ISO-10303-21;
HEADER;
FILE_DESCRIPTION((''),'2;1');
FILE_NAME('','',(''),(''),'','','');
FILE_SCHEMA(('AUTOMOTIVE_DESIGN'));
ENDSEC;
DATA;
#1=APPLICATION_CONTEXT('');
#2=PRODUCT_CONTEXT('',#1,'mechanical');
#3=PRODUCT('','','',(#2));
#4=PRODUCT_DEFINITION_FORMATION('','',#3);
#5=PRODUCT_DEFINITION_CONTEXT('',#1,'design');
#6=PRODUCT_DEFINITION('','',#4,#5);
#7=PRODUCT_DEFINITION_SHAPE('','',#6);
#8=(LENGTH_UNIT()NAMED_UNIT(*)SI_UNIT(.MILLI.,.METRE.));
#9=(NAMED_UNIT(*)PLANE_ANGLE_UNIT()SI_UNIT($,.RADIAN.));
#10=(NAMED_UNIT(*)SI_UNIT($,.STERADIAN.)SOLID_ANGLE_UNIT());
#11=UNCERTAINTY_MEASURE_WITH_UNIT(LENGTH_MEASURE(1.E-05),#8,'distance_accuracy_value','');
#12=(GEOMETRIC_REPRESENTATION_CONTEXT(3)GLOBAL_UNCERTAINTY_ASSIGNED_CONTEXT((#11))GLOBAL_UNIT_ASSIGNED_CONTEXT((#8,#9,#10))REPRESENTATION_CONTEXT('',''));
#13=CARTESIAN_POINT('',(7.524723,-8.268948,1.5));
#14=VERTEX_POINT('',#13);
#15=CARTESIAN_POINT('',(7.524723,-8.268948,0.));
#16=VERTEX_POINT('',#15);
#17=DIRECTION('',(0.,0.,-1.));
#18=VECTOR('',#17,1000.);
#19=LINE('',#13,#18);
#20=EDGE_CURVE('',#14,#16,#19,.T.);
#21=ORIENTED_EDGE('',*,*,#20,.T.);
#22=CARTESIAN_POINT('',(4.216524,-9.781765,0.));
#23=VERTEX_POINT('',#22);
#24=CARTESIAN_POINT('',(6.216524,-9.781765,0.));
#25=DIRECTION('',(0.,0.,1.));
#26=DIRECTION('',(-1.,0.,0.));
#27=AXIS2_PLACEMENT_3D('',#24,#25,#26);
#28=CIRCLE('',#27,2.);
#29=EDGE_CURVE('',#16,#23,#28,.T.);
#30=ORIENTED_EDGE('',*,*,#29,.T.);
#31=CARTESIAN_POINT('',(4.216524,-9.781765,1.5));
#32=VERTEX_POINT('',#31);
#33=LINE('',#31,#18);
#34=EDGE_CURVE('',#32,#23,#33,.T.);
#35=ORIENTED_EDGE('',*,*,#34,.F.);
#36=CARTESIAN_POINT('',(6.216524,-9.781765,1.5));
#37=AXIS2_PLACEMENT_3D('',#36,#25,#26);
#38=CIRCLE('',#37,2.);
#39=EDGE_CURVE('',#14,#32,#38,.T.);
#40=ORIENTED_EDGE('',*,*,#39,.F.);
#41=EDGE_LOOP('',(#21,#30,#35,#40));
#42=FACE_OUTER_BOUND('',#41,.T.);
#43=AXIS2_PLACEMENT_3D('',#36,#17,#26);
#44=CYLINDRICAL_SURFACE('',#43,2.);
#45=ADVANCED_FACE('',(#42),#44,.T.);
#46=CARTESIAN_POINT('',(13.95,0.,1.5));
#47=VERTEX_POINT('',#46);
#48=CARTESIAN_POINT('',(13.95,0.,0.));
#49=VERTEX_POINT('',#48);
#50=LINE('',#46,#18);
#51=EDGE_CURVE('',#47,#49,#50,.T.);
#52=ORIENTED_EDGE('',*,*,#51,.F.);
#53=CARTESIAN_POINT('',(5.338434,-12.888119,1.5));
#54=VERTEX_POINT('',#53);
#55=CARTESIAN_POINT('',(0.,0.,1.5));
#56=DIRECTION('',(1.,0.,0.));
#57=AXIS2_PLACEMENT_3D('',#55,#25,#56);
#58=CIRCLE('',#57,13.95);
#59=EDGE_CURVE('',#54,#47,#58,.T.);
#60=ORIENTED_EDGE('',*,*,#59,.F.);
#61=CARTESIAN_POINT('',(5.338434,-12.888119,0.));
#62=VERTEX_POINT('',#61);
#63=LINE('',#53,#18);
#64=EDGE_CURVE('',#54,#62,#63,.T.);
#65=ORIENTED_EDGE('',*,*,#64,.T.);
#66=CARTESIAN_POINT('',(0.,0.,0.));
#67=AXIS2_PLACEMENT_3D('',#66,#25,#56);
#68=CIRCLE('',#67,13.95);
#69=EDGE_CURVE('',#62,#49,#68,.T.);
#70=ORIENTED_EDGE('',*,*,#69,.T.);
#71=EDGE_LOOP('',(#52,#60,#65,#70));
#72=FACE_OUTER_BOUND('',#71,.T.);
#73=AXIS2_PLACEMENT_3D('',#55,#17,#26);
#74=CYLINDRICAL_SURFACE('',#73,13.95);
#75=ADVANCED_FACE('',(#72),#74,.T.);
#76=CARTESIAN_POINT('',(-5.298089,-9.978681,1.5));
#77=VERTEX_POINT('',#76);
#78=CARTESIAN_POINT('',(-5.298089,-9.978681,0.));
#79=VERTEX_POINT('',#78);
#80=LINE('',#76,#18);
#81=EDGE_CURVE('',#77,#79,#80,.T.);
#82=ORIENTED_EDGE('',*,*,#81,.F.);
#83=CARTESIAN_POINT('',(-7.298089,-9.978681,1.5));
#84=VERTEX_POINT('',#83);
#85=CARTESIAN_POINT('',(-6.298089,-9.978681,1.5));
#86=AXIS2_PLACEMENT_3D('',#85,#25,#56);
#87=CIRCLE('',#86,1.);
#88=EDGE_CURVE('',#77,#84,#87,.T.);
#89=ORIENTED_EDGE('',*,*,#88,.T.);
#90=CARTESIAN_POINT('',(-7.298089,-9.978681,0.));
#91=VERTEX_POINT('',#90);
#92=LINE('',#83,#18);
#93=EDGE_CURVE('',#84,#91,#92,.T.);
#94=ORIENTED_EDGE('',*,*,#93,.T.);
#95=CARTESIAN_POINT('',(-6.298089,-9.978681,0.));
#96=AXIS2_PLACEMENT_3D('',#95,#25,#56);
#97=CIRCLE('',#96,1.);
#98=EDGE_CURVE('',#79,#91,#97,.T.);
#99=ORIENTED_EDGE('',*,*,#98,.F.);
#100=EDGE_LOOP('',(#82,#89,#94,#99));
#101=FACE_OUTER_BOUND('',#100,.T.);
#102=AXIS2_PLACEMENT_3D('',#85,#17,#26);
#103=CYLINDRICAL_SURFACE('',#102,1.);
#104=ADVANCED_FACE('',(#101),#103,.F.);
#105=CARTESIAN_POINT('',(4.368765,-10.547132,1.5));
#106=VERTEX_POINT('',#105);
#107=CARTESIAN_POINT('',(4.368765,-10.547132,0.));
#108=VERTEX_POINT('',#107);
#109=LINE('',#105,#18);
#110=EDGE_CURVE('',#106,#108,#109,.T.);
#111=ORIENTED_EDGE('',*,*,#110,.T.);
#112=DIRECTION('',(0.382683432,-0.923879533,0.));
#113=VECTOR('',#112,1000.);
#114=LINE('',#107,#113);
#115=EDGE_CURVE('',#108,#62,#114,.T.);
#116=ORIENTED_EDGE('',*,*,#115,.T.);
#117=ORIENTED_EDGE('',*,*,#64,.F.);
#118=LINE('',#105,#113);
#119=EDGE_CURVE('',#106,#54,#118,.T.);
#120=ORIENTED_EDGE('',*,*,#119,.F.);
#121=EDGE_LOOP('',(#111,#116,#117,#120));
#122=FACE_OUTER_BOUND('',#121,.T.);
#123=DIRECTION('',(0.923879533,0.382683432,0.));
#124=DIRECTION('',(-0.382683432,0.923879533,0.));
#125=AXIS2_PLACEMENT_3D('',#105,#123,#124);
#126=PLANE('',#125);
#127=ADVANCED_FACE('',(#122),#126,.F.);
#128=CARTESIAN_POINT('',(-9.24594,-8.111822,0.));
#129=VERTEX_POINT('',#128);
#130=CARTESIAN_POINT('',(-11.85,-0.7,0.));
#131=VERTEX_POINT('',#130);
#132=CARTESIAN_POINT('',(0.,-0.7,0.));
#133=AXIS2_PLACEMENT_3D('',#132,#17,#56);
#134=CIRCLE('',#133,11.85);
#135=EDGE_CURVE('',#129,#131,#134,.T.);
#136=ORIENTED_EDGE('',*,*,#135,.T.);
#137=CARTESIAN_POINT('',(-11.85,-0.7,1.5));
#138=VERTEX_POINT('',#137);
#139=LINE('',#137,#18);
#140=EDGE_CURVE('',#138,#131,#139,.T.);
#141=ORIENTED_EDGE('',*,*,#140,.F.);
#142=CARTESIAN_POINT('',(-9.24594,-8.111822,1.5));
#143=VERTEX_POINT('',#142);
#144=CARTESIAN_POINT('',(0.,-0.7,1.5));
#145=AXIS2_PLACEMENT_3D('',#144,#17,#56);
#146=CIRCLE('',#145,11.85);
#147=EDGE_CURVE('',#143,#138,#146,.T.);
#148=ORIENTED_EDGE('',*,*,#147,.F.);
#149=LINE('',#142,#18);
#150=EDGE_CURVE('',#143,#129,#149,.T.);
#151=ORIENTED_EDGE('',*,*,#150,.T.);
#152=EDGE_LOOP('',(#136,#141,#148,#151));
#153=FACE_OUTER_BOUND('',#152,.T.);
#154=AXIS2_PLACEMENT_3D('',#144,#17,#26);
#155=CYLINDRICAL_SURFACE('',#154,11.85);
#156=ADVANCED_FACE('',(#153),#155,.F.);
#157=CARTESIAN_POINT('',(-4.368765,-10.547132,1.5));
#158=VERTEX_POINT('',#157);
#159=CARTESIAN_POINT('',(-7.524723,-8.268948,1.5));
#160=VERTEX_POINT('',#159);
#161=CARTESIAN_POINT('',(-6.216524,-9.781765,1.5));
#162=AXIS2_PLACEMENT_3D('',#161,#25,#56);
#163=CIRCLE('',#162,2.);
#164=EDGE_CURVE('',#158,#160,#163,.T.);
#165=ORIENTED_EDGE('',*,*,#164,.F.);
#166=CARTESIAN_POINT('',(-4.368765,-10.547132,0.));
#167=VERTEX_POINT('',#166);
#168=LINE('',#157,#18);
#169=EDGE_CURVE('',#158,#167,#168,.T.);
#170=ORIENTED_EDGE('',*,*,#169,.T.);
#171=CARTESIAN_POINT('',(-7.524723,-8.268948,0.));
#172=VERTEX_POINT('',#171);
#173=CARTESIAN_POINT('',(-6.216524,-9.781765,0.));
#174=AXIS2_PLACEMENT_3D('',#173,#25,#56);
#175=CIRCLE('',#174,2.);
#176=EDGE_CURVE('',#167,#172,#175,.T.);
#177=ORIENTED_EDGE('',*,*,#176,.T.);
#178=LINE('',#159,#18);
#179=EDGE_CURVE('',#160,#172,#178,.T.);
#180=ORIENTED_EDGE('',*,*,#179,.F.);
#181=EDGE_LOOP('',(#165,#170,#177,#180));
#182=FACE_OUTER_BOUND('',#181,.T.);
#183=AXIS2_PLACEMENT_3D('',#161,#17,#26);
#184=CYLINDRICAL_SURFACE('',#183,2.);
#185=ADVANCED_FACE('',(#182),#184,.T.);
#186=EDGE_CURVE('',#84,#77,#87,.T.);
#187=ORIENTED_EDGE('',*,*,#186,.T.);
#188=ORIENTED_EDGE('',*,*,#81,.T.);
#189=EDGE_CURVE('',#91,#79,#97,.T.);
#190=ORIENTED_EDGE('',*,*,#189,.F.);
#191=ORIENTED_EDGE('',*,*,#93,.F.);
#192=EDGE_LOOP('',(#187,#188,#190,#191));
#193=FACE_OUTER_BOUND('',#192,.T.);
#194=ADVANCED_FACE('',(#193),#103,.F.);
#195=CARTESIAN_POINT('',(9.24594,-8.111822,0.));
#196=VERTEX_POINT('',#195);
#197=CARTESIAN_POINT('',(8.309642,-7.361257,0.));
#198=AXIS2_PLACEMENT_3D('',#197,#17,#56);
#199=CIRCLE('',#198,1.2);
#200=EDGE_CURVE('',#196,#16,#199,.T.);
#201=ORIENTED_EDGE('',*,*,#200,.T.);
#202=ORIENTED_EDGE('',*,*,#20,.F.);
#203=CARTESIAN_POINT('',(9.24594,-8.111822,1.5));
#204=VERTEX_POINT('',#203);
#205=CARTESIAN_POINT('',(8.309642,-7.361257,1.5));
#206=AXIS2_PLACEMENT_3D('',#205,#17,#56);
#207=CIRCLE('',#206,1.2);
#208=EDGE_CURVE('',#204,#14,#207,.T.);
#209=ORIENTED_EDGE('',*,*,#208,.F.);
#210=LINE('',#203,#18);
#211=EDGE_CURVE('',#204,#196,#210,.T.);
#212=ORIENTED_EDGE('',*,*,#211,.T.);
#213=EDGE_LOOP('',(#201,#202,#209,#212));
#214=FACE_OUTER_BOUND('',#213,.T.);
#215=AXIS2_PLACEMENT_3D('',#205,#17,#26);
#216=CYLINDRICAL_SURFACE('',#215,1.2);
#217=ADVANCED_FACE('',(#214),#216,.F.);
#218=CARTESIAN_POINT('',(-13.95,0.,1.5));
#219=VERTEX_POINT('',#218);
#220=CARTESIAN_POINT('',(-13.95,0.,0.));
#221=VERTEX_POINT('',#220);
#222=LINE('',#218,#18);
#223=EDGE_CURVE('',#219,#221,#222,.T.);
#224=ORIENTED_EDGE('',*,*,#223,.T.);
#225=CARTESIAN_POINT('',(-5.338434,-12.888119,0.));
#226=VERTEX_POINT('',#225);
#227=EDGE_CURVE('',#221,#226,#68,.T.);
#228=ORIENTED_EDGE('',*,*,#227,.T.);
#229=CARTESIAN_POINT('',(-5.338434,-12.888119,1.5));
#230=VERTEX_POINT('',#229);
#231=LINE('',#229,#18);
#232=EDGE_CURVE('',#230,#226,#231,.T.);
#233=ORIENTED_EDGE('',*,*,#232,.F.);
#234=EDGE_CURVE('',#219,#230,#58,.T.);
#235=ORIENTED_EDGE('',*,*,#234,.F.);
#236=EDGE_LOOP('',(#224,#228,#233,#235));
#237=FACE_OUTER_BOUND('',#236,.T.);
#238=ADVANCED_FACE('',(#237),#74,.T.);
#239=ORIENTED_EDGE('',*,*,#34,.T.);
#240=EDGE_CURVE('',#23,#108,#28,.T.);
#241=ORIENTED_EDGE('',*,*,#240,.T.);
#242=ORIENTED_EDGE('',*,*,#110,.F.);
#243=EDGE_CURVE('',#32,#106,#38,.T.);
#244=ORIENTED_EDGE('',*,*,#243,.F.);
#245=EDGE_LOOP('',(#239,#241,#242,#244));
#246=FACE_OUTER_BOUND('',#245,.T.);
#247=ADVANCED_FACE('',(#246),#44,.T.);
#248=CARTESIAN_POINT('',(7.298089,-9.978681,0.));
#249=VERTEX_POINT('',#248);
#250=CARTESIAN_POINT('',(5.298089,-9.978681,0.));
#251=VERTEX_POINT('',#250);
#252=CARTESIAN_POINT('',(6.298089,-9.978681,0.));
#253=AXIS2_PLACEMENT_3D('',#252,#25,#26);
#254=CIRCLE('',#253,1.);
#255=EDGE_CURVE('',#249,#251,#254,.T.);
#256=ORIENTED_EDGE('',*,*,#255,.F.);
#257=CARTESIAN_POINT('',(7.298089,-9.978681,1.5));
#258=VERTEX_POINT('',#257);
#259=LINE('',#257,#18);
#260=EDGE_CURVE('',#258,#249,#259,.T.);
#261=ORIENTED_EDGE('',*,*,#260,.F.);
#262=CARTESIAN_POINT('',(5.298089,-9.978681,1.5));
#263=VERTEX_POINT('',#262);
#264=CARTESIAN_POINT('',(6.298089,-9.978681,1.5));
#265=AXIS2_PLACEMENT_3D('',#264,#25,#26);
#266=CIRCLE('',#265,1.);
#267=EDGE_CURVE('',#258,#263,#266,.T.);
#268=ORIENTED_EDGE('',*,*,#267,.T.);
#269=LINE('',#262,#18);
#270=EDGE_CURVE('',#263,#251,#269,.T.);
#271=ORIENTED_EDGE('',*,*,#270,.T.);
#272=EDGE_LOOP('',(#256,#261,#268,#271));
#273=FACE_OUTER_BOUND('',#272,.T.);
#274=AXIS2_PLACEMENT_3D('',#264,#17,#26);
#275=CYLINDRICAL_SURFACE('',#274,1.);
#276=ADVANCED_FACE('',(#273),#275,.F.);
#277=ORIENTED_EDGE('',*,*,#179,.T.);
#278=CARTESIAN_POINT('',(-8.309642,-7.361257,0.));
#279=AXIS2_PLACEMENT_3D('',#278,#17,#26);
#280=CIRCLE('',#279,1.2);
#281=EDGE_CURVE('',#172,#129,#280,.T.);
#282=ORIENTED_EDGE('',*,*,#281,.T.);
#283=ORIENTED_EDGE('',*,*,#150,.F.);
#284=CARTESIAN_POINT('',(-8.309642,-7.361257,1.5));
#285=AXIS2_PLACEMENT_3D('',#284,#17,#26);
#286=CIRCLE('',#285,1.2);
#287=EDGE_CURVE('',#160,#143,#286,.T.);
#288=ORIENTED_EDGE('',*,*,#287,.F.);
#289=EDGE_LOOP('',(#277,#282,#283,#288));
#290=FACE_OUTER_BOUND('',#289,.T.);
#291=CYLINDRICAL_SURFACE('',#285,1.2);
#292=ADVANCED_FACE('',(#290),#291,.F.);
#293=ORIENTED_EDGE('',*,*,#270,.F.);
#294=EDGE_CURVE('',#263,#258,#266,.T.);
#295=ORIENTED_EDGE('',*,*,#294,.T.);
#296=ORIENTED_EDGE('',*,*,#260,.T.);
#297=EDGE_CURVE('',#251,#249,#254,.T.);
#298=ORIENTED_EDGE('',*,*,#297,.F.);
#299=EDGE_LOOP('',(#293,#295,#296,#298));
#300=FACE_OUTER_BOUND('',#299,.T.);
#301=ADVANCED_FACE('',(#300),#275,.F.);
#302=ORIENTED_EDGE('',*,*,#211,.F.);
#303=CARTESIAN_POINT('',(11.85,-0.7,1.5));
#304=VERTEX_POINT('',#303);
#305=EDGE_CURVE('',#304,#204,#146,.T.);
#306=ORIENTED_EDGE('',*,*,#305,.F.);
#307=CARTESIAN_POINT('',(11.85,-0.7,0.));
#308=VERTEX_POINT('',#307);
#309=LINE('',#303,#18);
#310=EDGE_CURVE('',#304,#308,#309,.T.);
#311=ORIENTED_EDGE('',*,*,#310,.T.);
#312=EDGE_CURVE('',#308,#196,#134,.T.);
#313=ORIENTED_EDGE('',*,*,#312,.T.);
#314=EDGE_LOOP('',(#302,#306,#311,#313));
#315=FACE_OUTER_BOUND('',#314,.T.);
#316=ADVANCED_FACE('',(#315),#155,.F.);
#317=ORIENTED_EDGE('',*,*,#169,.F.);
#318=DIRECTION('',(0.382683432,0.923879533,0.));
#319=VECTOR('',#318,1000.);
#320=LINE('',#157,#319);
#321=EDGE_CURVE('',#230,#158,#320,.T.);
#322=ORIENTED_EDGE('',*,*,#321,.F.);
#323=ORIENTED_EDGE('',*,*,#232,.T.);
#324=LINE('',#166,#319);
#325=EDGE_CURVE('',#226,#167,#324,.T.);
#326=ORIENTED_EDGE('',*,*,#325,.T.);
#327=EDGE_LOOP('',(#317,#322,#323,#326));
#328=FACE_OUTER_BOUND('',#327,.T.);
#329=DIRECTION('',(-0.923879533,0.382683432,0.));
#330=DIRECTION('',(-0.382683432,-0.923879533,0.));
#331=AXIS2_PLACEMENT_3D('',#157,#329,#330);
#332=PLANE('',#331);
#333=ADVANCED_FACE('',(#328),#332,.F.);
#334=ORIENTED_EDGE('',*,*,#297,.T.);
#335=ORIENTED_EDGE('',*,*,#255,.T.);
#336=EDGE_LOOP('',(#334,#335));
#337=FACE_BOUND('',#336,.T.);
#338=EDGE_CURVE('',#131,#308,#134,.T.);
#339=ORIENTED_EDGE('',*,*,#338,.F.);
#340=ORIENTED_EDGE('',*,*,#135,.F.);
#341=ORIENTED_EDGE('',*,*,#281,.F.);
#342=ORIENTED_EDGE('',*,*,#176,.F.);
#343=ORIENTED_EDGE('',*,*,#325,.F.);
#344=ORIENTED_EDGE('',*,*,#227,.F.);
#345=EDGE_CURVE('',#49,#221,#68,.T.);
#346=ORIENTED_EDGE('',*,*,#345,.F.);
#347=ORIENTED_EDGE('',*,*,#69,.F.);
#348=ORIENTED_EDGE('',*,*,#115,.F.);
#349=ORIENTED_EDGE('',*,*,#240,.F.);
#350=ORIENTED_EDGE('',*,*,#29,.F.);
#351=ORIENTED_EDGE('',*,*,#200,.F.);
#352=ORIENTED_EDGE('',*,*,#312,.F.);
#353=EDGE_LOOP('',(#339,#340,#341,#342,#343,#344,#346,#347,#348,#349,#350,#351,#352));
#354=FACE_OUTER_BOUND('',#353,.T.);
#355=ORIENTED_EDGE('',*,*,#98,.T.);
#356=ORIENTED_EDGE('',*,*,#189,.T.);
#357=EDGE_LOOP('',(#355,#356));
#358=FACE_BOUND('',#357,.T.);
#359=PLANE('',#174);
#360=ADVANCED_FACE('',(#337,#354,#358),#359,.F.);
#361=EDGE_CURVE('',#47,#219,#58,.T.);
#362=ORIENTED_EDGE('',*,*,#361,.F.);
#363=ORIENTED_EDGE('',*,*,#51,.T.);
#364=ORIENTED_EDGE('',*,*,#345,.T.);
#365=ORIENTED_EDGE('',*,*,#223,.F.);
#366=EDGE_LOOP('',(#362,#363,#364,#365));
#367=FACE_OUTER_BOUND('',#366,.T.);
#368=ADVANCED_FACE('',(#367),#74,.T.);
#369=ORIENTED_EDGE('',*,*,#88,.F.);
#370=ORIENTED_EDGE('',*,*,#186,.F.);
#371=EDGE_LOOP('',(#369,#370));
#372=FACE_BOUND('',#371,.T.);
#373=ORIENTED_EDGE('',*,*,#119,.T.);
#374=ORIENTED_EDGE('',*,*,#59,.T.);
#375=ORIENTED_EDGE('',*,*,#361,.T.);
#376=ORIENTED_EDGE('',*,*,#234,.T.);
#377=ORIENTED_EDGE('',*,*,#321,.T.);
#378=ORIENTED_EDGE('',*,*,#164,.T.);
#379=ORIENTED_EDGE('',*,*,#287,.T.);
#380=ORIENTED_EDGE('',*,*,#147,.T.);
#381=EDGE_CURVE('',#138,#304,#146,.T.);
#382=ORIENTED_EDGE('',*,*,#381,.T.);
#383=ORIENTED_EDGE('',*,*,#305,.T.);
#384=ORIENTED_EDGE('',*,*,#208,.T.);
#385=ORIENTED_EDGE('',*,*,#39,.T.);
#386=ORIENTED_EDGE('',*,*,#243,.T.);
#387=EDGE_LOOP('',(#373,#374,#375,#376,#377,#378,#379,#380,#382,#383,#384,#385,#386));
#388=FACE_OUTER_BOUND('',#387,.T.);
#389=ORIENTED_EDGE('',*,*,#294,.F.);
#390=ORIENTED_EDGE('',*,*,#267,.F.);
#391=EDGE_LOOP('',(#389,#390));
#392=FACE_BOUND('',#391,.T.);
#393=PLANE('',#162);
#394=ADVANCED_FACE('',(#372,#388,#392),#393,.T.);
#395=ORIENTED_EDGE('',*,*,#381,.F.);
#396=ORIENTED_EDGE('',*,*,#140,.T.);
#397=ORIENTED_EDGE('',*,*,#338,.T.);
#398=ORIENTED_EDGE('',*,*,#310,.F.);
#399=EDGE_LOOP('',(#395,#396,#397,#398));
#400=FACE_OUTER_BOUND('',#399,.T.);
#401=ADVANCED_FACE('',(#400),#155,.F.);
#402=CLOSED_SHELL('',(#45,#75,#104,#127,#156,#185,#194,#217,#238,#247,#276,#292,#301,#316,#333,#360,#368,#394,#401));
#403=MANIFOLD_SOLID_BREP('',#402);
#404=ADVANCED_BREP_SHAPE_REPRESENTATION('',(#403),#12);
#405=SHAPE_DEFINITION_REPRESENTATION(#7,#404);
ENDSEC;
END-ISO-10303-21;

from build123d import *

# Parameters (mm, degrees)
SKETCH_1_R        = 1
EXTRUDE_967_DEPTH = 1.5


with BuildPart() as part:
    # 草图1 → Extrude 967 (new body)
    with BuildSketch(Plane.XY):
        with BuildLine():
            Line((-4.368765084, -10.547131916), (-5.338433881, -12.888119479))
            ThreePointArc((-5.338433881, -12.888119479), (0, 13.95), (5.338433881, -12.888119479))
            Line((5.338433881, -12.888119479), (4.368765084, -10.547131916))
            ThreePointArc((4.368765084, -10.547131916), (5.045920823, -8.160133818), (7.524722821, -8.268947735))
            ThreePointArc((7.524722821, -8.268947735), (8.418733826, -8.556288298), (9.245939718, -8.111821553))
            ThreePointArc((9.245939718, -8.111821553), (0, 11.15), (-9.245939718, -8.111821553))
            ThreePointArc((-9.245939718, -8.111821553), (-8.418733826, -8.556288298), (-7.524722821, -8.268947735))
            ThreePointArc((-7.524722821, -8.268947735), (-5.045920823, -8.160133818), (-4.368765084, -10.547131916))
        make_face()
        with Locations((-6.298089329, -9.978680815)):
            Circle(SKETCH_1_R, mode=Mode.SUBTRACT)
        with Locations(Location((6.298089329, -9.978680815, 0), (0, 0, 180))):
            Circle(SKETCH_1_R, mode=Mode.SUBTRACT)
    extrude(amount=EXTRUDE_967_DEPTH)


solid = part.part
